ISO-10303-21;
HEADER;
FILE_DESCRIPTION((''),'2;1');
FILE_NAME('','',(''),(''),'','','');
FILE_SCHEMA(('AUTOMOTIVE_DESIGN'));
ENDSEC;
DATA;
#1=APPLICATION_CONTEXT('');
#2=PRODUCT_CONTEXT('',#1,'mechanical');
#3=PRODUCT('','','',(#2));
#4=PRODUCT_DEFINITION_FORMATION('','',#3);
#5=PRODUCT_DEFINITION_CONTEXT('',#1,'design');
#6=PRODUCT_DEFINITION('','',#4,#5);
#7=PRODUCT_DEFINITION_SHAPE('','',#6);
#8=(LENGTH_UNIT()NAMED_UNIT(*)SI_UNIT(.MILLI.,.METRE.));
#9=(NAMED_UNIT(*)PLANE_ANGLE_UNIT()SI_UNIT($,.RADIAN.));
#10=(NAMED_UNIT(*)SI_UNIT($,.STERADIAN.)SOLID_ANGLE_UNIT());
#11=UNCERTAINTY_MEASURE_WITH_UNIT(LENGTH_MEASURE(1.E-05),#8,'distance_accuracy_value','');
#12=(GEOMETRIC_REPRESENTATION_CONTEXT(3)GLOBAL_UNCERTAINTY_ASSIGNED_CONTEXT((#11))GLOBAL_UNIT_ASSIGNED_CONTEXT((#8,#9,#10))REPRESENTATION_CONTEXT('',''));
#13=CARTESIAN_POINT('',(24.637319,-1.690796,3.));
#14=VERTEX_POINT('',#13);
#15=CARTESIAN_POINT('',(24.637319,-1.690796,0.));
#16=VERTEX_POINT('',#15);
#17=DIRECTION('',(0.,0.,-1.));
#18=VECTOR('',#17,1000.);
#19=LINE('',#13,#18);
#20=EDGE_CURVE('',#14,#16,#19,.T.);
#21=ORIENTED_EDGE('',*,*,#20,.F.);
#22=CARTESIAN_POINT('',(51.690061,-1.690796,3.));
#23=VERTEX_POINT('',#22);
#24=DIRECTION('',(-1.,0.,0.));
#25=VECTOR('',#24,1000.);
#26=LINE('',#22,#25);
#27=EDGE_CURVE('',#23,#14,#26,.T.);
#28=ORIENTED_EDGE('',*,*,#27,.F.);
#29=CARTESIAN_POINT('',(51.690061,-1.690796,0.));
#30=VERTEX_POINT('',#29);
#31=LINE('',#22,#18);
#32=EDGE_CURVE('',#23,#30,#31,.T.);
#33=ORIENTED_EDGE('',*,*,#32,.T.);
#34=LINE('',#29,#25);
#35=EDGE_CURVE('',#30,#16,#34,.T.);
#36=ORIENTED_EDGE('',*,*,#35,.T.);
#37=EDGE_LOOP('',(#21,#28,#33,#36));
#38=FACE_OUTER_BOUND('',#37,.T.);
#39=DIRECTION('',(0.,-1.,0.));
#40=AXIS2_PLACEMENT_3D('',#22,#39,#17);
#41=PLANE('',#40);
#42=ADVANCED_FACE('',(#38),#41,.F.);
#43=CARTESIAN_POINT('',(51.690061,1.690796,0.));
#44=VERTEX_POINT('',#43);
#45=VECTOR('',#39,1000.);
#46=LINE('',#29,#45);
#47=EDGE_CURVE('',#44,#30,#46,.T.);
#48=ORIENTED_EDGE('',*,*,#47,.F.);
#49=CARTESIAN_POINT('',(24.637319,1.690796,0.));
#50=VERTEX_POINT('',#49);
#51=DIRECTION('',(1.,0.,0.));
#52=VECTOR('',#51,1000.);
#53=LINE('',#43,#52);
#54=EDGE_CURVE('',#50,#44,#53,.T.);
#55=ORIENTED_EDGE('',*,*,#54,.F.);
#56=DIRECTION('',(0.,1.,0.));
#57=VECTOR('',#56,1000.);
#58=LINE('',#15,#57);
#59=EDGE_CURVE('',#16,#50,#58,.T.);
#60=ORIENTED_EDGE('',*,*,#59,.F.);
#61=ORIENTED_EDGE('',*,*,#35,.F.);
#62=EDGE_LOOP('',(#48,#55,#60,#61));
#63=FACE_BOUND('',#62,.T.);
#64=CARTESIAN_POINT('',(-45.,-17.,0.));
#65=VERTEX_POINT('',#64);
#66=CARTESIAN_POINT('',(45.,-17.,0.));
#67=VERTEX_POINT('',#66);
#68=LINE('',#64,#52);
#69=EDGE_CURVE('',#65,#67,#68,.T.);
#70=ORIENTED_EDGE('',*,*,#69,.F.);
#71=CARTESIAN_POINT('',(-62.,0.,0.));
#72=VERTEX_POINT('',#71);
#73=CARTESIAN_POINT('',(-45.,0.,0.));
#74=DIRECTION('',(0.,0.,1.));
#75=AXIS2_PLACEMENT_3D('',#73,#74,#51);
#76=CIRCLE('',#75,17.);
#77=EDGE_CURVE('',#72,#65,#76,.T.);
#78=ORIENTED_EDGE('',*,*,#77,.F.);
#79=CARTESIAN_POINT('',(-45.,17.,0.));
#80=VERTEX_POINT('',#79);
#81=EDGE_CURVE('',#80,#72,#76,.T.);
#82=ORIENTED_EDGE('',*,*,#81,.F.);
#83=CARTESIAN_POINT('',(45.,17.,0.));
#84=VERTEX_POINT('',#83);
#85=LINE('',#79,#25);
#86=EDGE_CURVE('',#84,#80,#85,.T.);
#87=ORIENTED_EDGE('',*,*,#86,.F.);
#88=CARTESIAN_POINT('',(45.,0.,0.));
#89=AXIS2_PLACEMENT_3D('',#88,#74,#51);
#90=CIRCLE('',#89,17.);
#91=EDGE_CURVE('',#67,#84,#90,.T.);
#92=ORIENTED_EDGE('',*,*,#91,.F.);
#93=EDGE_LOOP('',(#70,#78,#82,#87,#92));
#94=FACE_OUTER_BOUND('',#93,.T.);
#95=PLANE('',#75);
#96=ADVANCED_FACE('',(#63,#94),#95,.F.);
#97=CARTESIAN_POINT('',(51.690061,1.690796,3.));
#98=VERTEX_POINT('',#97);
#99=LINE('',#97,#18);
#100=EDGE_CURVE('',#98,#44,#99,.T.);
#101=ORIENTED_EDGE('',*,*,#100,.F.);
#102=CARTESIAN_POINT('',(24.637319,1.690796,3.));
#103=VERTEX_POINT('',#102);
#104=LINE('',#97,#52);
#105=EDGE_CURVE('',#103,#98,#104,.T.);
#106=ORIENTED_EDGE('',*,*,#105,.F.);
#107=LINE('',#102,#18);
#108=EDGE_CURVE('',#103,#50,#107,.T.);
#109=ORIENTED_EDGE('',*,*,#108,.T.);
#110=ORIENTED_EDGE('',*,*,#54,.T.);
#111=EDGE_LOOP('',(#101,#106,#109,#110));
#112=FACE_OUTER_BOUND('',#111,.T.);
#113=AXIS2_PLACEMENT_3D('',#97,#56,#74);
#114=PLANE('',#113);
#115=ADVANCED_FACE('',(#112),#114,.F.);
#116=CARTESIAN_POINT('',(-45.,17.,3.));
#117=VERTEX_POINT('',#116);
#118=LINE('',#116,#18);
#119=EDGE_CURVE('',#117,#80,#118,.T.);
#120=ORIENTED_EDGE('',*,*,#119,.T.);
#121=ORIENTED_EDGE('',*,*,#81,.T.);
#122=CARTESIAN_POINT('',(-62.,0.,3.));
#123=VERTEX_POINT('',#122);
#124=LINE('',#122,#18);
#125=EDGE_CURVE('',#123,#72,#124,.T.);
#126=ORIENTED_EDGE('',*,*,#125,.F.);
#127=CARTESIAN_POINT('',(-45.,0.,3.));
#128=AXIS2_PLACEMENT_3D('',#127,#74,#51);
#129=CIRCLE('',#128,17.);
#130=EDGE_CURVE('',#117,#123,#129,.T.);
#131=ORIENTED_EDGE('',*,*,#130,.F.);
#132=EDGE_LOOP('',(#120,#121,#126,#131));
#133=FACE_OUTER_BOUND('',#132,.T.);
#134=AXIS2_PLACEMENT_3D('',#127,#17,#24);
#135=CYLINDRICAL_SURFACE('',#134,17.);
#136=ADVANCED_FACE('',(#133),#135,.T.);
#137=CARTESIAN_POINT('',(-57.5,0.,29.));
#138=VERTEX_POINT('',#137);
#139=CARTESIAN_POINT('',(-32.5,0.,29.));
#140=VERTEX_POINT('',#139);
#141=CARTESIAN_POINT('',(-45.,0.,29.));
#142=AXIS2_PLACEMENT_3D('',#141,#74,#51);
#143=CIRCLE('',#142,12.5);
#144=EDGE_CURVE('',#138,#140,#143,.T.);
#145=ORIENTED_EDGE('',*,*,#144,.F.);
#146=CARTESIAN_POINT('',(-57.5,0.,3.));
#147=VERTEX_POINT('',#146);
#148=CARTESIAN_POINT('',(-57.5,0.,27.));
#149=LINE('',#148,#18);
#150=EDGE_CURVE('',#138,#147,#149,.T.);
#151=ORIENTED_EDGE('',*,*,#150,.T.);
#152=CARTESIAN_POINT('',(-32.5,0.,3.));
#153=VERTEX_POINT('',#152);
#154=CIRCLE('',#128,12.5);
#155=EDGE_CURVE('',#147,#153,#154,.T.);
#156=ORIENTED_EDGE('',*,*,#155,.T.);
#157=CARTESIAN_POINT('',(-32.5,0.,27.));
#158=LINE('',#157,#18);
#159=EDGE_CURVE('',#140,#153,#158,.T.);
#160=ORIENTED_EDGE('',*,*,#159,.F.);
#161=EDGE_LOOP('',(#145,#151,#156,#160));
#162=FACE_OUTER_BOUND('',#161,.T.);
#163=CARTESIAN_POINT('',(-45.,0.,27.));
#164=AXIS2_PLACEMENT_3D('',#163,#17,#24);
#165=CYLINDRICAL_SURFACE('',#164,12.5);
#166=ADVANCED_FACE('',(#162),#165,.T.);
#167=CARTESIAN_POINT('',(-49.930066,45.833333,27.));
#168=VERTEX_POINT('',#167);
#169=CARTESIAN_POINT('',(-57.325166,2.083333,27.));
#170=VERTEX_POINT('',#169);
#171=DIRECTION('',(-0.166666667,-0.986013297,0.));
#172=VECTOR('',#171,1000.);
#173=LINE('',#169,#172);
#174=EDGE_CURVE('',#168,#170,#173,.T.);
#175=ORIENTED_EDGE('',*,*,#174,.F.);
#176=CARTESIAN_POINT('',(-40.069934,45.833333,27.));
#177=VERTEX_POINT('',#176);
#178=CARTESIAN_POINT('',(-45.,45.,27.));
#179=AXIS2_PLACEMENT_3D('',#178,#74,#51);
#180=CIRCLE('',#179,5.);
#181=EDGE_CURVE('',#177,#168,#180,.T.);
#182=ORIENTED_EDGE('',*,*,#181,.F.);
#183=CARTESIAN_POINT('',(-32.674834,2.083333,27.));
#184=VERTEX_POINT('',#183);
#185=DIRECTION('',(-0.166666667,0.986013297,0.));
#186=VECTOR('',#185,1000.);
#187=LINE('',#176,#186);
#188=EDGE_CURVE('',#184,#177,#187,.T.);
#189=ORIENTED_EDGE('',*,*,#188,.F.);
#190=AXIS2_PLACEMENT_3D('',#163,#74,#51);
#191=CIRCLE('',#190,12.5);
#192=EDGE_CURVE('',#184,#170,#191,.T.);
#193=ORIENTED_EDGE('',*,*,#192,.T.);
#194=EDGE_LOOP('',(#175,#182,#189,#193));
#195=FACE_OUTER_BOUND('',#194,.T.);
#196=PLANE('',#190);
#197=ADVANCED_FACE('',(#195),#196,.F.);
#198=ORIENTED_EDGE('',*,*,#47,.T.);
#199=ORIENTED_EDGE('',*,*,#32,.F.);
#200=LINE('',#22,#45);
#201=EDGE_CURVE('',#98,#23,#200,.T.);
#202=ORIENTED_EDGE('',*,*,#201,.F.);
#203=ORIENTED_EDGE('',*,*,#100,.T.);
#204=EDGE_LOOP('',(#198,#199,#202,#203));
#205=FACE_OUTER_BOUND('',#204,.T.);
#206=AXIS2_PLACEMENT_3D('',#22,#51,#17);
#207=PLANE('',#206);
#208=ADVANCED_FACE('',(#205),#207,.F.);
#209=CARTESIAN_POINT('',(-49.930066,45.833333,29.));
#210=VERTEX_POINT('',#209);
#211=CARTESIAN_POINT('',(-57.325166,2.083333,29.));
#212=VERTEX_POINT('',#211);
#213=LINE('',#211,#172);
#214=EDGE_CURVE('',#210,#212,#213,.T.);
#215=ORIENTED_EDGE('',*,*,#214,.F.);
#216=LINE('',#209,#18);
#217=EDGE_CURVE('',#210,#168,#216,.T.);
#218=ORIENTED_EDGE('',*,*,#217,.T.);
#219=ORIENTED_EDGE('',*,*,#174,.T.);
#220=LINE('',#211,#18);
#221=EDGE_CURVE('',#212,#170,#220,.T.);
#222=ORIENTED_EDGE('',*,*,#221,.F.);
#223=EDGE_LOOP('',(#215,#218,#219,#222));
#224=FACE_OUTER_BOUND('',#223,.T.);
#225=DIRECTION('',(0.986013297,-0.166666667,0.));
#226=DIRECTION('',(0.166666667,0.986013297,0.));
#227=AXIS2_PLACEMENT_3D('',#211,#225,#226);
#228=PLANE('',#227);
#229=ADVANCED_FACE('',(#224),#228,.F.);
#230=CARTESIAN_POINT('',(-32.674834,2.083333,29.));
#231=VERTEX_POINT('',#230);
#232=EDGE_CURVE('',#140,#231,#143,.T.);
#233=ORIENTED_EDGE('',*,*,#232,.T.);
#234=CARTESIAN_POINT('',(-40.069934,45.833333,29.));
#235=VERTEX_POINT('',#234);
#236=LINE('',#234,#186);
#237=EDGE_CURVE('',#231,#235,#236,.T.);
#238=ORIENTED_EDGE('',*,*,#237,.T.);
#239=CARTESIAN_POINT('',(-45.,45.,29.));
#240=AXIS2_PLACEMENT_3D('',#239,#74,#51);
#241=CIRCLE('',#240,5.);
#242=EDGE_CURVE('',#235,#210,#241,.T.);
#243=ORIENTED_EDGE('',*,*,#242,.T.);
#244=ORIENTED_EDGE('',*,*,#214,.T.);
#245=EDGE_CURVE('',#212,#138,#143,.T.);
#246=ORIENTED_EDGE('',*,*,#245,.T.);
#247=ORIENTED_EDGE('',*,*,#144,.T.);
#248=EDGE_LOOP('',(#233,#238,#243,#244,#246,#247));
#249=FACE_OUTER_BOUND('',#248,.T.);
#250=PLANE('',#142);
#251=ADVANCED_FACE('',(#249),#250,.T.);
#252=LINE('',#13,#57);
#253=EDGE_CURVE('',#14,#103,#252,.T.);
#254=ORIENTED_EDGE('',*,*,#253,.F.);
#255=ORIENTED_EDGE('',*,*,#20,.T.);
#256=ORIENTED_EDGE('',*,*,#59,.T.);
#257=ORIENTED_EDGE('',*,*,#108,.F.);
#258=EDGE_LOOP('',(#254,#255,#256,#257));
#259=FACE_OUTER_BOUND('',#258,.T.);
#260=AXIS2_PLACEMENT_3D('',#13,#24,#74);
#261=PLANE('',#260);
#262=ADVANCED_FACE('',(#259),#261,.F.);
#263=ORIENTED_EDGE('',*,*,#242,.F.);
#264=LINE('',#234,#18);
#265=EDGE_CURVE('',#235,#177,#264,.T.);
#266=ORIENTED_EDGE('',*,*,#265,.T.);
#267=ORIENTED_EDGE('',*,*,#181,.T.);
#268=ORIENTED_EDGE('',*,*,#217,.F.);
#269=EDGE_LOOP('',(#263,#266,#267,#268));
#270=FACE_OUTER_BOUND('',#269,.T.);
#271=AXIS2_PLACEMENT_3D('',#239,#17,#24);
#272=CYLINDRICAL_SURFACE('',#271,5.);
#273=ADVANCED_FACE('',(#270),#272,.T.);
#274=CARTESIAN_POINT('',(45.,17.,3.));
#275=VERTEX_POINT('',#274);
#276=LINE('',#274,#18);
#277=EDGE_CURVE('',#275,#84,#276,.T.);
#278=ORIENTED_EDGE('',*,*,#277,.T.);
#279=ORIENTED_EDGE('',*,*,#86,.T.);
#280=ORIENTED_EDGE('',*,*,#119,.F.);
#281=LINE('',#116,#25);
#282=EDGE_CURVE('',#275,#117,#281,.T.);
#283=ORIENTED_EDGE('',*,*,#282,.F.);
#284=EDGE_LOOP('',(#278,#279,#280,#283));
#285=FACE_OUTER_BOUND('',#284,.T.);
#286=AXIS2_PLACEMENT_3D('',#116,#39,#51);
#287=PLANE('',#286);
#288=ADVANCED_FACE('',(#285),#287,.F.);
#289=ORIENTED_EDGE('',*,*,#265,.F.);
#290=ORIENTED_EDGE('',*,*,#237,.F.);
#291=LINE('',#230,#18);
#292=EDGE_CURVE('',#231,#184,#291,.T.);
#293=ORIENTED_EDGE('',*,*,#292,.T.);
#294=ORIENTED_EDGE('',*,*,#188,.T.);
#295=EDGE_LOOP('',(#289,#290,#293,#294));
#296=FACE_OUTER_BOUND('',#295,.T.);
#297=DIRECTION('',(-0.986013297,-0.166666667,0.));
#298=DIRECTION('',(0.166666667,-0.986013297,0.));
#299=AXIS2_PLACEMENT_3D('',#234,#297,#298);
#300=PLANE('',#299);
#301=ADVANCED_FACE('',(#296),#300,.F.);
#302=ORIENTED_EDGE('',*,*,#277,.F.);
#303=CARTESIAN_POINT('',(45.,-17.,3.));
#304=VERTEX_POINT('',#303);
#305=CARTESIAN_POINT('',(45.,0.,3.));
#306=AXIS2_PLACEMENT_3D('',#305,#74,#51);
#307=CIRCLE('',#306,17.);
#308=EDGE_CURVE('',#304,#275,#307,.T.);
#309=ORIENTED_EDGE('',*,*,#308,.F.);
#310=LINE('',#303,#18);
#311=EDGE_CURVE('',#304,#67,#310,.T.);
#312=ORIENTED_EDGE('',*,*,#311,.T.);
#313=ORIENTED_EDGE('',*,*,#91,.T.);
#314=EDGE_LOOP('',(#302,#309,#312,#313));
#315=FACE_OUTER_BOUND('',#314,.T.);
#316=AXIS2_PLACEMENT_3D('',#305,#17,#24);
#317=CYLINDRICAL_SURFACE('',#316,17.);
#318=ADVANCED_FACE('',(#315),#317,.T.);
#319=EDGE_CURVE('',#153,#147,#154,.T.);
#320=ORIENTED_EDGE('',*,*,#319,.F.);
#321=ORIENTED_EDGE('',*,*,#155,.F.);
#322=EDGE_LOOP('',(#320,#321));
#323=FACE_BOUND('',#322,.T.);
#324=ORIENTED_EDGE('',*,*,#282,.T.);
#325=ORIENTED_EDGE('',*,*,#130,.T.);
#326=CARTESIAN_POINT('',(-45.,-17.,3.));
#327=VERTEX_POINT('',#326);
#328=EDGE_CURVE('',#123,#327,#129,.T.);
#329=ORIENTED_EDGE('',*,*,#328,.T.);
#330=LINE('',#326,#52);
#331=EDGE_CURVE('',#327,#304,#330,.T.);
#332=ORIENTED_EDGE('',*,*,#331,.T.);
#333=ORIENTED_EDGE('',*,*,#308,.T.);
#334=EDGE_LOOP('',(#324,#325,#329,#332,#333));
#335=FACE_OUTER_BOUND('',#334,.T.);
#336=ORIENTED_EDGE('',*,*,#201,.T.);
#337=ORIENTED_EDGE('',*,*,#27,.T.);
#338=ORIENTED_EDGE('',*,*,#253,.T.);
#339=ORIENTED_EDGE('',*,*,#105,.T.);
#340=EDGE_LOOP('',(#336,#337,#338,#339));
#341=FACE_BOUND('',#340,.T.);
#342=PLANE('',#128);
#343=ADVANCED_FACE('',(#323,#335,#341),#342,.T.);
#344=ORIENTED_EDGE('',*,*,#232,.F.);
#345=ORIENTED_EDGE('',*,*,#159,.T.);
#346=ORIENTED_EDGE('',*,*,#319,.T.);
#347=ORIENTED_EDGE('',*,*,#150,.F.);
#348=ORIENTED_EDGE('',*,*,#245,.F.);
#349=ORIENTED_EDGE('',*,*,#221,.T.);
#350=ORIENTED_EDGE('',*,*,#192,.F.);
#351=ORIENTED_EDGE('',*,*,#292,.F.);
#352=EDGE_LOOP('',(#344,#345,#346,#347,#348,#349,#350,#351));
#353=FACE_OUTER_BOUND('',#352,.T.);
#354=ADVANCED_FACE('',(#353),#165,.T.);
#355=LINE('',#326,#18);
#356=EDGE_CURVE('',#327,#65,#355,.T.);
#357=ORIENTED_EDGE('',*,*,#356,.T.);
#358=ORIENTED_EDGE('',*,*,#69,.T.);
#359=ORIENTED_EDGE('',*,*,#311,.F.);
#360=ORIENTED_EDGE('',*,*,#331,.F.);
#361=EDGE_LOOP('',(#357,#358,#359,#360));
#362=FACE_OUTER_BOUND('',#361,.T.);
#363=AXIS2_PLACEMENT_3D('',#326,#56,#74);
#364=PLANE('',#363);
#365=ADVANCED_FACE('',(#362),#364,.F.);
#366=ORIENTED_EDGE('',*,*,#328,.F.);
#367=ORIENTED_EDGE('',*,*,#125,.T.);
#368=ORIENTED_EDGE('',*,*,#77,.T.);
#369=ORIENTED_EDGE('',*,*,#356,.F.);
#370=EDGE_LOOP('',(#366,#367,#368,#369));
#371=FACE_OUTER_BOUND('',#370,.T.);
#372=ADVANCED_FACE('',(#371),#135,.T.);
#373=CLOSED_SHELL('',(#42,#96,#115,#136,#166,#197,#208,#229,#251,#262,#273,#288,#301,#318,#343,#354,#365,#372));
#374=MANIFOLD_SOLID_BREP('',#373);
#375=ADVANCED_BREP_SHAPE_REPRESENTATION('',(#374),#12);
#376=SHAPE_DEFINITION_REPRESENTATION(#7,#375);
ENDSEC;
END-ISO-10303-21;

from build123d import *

# Parameters (mm, degrees)
EXTRUDE_1_DEPTH     = 3
SKETCH_2_W          = 27.052742461
SKETCH_2_H          = 3.381592808
CUT_EXTRUDE_1_DEPTH = 3
SKETCH_3_R          = 12.5
EXTRUDE_2_DEPTH     = 24
EXTRUDE_3_DEPTH     = 2


with BuildPart() as part:
    # 草图1 → 凸台-拉伸1 (new body)
    with BuildSketch(Plane.XY):
        with BuildLine():
            Line((-45, 17), (45, 17))
            ThreePointArc((45, 17), (62, 0), (45, -17))
            Line((45, -17), (-45, -17))
            ThreePointArc((-45, -17), (-62, 0), (-45, 17))
        make_face()
    extrude(amount=EXTRUDE_1_DEPTH)

    # 草图2 → 切除-拉伸1 (cut)
    with BuildSketch(Plane(origin=(0, 0, 0), x_dir=(-1, 0, 0), z_dir=(0, 0, -1))):
        with Locations((-38.163690258, 0)):
            Rectangle(SKETCH_2_W, SKETCH_2_H)
    extrude(amount=-CUT_EXTRUDE_1_DEPTH, mode=Mode.SUBTRACT)

    # 草图3 → 凸台-拉伸2 (add)
    with BuildSketch(Plane.XY.offset(3)):
        with Locations((-45, 0)):
            Circle(SKETCH_3_R)
    extrude(amount=EXTRUDE_2_DEPTH)

    # 草图4 → 凸台-拉伸3 (add)
    with BuildSketch(Plane.XY.offset(27)):
        with BuildLine():
            Line((-57.325166215, 2.083333333), (-49.930066486, 45.833333333))
            ThreePointArc((-49.930066486, 45.833333333), (-45, 50), (-40.069933514, 45.833333333))
            Line((-40.069933514, 45.833333333), (-32.674833785, 2.083333333))
            ThreePointArc((-32.674833785, 2.083333333), (-45, -12.5), (-57.325166215, 2.083333333))
        make_face()
    extrude(amount=EXTRUDE_3_DEPTH)


solid = part.part
